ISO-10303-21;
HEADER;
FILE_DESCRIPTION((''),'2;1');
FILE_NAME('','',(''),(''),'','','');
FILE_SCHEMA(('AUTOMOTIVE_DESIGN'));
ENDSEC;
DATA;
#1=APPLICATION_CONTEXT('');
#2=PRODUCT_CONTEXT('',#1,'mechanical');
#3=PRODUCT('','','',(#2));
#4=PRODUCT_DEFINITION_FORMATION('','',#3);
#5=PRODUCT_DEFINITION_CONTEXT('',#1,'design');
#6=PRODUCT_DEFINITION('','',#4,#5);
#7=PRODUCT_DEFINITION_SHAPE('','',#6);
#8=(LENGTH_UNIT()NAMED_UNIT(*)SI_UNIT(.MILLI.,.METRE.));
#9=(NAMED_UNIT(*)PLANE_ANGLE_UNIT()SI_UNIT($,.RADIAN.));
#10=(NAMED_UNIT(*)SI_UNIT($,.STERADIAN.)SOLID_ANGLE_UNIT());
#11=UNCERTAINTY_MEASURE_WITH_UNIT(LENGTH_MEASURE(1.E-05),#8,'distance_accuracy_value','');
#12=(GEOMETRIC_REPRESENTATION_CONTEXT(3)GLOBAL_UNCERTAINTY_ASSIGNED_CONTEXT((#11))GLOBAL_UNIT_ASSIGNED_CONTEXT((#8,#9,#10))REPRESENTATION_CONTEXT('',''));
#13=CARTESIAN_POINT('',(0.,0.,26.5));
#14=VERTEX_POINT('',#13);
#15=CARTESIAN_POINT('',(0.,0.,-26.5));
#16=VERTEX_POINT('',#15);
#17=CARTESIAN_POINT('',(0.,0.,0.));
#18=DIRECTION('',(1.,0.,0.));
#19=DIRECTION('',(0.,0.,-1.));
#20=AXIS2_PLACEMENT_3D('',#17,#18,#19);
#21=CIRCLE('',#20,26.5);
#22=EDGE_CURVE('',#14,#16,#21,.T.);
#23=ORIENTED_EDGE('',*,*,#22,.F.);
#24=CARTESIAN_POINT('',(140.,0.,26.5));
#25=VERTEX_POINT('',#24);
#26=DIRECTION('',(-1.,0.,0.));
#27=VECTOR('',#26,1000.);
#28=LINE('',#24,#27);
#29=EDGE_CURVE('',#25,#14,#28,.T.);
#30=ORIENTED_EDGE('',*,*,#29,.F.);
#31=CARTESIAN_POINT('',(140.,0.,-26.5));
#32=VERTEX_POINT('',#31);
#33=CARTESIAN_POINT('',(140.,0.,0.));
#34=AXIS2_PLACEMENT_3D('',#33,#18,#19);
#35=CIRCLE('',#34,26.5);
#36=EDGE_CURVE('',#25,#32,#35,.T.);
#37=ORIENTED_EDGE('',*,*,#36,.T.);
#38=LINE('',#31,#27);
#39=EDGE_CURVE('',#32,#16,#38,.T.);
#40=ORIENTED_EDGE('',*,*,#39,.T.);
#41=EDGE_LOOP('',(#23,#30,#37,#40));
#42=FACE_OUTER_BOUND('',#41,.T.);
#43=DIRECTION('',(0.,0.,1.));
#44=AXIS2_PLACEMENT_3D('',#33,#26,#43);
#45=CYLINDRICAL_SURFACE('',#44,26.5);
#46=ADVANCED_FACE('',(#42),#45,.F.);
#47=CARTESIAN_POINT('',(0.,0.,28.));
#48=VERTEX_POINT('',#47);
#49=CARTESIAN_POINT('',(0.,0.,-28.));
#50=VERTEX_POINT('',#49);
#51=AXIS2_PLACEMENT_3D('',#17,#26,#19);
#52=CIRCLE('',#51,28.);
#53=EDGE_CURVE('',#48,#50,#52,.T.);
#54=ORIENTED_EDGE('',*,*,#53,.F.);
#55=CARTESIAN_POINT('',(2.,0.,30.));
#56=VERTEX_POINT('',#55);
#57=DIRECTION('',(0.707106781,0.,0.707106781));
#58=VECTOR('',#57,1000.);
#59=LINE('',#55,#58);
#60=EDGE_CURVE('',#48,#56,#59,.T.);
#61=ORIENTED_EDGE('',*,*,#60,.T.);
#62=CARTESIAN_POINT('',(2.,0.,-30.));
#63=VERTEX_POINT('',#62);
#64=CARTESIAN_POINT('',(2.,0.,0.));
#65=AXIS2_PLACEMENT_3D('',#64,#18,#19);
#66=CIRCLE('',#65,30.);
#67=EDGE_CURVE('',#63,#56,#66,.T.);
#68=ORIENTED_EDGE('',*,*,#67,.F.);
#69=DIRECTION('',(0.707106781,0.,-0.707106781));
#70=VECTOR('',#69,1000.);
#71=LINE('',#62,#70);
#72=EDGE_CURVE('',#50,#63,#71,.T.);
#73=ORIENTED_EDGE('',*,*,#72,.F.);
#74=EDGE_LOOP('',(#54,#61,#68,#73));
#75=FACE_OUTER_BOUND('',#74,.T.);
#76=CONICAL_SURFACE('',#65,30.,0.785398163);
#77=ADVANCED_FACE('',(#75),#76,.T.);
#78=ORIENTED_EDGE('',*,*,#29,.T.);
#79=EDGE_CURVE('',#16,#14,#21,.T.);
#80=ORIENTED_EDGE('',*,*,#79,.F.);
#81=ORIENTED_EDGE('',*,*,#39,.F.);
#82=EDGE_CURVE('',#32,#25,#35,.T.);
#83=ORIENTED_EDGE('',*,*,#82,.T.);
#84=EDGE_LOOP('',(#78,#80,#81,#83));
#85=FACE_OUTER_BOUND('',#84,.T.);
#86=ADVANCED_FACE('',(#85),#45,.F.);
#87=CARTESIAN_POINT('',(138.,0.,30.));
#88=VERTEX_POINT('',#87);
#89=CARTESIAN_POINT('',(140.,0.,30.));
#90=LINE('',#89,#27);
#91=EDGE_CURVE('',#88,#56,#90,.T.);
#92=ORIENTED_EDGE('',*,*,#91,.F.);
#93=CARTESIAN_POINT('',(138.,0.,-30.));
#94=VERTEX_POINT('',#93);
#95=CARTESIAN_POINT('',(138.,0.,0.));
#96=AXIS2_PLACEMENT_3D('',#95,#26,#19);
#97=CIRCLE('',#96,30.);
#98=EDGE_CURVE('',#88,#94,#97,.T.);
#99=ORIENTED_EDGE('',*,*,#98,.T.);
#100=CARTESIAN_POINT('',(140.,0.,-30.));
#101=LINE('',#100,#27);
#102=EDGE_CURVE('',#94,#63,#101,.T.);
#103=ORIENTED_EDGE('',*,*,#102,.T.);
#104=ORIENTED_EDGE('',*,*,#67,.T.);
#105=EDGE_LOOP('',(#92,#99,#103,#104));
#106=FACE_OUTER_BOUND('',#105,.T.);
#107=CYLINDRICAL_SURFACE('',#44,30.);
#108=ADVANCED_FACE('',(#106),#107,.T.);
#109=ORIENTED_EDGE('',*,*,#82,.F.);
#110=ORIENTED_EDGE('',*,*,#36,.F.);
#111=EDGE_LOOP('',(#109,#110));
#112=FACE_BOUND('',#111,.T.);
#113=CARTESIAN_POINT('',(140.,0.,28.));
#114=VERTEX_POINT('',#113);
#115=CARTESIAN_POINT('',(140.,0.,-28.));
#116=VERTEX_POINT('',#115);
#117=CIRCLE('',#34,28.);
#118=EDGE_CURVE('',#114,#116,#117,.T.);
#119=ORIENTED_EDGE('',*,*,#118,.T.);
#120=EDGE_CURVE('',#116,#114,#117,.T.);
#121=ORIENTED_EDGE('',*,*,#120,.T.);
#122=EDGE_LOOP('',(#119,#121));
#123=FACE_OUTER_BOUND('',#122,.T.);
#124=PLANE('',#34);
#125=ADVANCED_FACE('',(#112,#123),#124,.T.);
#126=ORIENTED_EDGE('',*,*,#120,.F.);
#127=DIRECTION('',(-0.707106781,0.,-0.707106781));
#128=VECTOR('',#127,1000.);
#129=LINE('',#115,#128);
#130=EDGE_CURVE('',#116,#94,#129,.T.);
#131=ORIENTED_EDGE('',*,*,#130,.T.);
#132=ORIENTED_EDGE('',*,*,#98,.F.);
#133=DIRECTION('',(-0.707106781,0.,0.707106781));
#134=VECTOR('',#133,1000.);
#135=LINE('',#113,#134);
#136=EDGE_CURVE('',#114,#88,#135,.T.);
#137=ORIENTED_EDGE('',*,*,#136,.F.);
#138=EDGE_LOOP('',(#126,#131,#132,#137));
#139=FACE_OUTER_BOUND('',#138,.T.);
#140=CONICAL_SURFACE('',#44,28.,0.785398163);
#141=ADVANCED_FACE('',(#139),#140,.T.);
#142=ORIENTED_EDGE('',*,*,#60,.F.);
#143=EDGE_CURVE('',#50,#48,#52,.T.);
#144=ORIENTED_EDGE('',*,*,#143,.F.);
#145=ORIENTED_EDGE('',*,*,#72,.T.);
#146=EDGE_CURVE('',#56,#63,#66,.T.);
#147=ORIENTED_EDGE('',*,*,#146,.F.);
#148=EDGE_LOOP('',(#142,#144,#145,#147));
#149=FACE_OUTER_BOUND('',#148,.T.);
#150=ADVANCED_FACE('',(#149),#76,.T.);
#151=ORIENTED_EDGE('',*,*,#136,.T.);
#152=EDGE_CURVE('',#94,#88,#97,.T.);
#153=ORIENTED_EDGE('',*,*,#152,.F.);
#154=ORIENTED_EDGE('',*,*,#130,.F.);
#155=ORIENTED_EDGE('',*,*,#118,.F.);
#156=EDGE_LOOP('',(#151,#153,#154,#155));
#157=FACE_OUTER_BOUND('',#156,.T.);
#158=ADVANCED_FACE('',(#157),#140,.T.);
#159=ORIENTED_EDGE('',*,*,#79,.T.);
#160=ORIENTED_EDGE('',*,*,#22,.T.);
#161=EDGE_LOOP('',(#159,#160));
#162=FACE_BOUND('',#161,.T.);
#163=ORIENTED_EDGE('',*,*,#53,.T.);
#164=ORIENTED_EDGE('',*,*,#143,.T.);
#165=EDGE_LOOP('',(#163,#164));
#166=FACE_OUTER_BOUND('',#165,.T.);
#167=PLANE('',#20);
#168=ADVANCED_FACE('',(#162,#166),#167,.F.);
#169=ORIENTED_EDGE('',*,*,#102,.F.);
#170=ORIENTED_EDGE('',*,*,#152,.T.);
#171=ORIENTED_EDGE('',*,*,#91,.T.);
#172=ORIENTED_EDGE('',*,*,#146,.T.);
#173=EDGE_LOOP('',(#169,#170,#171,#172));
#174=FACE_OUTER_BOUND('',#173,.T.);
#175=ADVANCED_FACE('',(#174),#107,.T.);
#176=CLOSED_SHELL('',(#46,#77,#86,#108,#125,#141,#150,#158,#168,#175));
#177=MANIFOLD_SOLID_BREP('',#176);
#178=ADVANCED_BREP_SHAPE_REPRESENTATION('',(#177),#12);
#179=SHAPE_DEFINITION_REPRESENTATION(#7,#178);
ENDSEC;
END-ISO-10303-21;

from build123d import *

# Parameters (mm, degrees)
SKETCH_1_R      = 30
SKETCH_1_R_2    = 26.5
EXTRUDE_1_DEPTH = 140
CHAMFER_1_SIZE  = 2


with BuildPart() as part:
    # 草图1 → 拉伸-薄壁1 (new body)
    with BuildSketch(Plane(origin=(0, 0, 0), x_dir=(0, 0, -1), z_dir=(1, 0, 0))):
        Circle(SKETCH_1_R)
        Circle(SKETCH_1_R_2, mode=Mode.SUBTRACT)
    extrude(amount=EXTRUDE_1_DEPTH)

    # 倒角1
    chamfer_1_edges = [part.edges().sort_by_distance(p)[0] for p in [
        (0, 0, 30),
        (140, 0, 30),
    ]]
    chamfer(chamfer_1_edges, length=CHAMFER_1_SIZE)


solid = part.part
